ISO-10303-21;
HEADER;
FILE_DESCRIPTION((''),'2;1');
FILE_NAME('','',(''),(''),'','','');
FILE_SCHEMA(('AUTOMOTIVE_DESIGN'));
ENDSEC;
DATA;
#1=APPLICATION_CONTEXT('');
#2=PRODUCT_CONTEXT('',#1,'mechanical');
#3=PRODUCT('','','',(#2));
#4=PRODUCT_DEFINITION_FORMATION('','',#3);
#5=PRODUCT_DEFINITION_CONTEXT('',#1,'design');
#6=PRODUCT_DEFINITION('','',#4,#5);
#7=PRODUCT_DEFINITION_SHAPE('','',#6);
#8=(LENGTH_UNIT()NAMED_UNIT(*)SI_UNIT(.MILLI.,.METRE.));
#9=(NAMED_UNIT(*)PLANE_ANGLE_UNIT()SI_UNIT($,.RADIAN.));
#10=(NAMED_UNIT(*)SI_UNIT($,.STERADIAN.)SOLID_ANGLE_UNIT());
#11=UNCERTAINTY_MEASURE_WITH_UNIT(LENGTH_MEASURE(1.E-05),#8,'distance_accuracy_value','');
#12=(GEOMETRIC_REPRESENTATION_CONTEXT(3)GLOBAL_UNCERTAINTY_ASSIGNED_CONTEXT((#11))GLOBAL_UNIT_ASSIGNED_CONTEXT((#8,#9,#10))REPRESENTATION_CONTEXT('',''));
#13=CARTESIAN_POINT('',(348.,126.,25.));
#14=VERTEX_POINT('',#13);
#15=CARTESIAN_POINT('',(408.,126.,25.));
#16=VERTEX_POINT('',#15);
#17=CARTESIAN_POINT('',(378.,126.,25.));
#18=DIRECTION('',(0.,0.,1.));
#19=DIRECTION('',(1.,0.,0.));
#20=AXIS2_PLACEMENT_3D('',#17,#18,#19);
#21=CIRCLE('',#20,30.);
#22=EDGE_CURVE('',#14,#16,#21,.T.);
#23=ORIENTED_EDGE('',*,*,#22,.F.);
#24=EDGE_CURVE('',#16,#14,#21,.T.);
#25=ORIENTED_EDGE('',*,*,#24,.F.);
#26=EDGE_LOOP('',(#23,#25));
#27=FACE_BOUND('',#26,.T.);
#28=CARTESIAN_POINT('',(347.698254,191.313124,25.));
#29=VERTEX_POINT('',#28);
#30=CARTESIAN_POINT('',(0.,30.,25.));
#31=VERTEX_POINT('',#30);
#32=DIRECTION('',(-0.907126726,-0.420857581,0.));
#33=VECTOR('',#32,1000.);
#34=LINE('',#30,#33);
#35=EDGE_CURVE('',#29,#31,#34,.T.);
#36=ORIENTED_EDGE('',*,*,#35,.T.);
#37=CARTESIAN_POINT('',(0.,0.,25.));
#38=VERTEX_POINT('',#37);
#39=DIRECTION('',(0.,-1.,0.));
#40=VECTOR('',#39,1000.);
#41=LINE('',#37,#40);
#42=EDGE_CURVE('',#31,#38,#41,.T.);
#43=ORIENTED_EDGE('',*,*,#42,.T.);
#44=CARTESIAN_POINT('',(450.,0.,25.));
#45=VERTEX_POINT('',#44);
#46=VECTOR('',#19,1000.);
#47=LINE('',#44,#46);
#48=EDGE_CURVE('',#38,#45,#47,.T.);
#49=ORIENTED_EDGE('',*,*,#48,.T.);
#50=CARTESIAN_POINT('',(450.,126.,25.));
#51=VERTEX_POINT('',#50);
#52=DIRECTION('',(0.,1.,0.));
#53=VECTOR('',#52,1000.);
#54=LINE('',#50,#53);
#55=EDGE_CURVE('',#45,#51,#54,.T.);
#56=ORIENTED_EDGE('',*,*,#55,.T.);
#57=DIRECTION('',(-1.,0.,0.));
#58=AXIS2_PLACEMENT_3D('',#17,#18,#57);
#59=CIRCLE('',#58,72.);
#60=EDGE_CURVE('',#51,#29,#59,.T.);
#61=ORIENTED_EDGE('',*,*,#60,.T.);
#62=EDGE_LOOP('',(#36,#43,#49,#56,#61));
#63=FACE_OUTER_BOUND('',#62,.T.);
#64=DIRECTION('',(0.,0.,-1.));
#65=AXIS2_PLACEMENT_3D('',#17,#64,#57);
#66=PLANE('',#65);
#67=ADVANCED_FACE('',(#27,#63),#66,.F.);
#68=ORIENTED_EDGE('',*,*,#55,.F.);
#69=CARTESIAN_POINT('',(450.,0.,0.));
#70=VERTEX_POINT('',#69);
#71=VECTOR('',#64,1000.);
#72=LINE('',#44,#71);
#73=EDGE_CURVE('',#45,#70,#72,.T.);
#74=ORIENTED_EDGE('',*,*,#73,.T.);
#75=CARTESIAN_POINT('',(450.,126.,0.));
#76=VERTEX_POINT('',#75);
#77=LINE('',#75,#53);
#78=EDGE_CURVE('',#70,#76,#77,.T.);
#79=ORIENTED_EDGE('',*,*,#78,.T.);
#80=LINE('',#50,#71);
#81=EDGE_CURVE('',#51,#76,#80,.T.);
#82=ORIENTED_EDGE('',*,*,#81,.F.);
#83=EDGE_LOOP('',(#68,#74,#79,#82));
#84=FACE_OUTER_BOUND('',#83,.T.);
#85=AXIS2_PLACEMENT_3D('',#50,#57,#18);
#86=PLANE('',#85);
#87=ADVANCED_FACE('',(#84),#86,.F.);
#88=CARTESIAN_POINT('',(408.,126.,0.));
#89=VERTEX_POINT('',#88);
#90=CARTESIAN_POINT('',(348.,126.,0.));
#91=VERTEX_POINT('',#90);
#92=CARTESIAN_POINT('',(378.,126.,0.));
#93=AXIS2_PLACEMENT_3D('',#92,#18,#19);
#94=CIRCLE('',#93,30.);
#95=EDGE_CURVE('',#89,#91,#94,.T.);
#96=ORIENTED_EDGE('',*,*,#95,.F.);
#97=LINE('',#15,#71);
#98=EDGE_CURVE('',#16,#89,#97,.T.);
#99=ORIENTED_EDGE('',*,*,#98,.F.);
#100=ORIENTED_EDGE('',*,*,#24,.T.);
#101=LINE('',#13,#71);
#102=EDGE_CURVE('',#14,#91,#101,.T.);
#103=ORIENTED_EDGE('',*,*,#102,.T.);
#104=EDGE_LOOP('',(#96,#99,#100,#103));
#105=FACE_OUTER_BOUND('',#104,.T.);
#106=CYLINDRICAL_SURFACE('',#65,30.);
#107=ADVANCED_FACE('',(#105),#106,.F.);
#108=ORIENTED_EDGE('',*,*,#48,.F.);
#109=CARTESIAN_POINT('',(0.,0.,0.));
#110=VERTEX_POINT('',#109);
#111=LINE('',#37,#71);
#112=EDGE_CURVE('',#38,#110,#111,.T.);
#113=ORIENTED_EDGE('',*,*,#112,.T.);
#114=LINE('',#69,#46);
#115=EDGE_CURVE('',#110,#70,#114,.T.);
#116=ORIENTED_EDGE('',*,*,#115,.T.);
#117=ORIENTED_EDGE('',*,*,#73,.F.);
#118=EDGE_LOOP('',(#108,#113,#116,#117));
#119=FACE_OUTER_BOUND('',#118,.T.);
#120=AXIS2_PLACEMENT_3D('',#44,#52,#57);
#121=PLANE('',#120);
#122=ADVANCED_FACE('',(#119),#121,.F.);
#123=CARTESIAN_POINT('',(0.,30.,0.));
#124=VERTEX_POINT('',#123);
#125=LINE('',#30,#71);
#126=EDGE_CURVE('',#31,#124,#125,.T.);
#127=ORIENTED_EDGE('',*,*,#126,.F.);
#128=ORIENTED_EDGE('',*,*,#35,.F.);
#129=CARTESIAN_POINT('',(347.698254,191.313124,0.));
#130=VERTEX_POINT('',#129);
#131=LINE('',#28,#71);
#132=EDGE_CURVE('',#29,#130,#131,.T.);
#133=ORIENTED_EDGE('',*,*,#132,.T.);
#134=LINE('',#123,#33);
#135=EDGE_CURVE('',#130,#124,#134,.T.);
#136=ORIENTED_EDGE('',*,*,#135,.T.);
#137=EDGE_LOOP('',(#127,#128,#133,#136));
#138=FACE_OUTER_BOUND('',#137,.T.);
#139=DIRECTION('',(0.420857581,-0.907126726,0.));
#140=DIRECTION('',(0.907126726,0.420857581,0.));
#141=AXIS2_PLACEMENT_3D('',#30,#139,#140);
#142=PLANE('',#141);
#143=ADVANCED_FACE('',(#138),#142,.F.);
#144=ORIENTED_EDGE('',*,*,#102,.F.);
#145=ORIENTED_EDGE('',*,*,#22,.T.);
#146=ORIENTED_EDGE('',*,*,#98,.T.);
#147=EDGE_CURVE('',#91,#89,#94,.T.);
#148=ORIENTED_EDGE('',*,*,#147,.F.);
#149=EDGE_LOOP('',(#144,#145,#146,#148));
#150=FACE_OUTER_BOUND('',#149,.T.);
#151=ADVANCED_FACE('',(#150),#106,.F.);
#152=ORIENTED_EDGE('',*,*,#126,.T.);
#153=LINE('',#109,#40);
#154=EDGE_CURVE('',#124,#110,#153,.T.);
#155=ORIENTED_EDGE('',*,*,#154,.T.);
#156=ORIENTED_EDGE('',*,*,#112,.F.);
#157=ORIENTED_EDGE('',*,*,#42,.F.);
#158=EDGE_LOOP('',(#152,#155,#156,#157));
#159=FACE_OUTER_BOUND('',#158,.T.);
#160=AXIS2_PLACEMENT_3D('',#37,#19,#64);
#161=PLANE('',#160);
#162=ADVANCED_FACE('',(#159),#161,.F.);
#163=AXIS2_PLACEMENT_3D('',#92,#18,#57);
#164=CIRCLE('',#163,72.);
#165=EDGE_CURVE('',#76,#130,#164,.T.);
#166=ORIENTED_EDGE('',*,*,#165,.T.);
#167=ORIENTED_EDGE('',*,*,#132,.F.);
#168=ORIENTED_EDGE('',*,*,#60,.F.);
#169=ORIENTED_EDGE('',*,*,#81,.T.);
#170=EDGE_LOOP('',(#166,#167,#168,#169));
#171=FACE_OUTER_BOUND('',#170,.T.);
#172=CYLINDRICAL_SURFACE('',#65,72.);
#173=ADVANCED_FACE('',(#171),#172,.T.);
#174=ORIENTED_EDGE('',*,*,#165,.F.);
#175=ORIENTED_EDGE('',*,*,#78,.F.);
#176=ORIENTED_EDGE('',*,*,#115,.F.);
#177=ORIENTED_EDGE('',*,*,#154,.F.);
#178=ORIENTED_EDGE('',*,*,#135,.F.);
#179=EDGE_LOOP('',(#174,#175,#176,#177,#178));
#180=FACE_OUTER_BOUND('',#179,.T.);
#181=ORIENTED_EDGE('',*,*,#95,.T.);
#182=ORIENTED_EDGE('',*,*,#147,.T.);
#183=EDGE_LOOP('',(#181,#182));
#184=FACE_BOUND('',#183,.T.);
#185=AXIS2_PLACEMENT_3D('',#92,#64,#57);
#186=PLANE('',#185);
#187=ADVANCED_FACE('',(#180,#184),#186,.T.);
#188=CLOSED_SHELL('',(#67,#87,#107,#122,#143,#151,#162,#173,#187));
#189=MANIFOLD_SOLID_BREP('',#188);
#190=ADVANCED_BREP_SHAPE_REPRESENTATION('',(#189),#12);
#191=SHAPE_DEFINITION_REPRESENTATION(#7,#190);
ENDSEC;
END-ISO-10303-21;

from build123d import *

# Parameters (mm, degrees)
SKETCH1_R           = 30
BOSS_EXTRUDE1_DEPTH = 25


with BuildPart() as part:
    # Sketch1 → Boss-Extrude1 (new body)
    with BuildSketch(Plane.XY):
        with BuildLine():
            Line((0, 0), (0, 30))
            Line((0, 30), (347.698254159, 191.313124248))
            ThreePointArc((347.698254159, 191.313124248), (416.744511221, 186.68659531), (450, 126))
            Line((450, 126), (450, 0))
            Line((450, 0), (0, 0))
        make_face()
        with Locations((378, 126)):
            Circle(SKETCH1_R, mode=Mode.SUBTRACT)
    extrude(amount=BOSS_EXTRUDE1_DEPTH)


solid = part.part
